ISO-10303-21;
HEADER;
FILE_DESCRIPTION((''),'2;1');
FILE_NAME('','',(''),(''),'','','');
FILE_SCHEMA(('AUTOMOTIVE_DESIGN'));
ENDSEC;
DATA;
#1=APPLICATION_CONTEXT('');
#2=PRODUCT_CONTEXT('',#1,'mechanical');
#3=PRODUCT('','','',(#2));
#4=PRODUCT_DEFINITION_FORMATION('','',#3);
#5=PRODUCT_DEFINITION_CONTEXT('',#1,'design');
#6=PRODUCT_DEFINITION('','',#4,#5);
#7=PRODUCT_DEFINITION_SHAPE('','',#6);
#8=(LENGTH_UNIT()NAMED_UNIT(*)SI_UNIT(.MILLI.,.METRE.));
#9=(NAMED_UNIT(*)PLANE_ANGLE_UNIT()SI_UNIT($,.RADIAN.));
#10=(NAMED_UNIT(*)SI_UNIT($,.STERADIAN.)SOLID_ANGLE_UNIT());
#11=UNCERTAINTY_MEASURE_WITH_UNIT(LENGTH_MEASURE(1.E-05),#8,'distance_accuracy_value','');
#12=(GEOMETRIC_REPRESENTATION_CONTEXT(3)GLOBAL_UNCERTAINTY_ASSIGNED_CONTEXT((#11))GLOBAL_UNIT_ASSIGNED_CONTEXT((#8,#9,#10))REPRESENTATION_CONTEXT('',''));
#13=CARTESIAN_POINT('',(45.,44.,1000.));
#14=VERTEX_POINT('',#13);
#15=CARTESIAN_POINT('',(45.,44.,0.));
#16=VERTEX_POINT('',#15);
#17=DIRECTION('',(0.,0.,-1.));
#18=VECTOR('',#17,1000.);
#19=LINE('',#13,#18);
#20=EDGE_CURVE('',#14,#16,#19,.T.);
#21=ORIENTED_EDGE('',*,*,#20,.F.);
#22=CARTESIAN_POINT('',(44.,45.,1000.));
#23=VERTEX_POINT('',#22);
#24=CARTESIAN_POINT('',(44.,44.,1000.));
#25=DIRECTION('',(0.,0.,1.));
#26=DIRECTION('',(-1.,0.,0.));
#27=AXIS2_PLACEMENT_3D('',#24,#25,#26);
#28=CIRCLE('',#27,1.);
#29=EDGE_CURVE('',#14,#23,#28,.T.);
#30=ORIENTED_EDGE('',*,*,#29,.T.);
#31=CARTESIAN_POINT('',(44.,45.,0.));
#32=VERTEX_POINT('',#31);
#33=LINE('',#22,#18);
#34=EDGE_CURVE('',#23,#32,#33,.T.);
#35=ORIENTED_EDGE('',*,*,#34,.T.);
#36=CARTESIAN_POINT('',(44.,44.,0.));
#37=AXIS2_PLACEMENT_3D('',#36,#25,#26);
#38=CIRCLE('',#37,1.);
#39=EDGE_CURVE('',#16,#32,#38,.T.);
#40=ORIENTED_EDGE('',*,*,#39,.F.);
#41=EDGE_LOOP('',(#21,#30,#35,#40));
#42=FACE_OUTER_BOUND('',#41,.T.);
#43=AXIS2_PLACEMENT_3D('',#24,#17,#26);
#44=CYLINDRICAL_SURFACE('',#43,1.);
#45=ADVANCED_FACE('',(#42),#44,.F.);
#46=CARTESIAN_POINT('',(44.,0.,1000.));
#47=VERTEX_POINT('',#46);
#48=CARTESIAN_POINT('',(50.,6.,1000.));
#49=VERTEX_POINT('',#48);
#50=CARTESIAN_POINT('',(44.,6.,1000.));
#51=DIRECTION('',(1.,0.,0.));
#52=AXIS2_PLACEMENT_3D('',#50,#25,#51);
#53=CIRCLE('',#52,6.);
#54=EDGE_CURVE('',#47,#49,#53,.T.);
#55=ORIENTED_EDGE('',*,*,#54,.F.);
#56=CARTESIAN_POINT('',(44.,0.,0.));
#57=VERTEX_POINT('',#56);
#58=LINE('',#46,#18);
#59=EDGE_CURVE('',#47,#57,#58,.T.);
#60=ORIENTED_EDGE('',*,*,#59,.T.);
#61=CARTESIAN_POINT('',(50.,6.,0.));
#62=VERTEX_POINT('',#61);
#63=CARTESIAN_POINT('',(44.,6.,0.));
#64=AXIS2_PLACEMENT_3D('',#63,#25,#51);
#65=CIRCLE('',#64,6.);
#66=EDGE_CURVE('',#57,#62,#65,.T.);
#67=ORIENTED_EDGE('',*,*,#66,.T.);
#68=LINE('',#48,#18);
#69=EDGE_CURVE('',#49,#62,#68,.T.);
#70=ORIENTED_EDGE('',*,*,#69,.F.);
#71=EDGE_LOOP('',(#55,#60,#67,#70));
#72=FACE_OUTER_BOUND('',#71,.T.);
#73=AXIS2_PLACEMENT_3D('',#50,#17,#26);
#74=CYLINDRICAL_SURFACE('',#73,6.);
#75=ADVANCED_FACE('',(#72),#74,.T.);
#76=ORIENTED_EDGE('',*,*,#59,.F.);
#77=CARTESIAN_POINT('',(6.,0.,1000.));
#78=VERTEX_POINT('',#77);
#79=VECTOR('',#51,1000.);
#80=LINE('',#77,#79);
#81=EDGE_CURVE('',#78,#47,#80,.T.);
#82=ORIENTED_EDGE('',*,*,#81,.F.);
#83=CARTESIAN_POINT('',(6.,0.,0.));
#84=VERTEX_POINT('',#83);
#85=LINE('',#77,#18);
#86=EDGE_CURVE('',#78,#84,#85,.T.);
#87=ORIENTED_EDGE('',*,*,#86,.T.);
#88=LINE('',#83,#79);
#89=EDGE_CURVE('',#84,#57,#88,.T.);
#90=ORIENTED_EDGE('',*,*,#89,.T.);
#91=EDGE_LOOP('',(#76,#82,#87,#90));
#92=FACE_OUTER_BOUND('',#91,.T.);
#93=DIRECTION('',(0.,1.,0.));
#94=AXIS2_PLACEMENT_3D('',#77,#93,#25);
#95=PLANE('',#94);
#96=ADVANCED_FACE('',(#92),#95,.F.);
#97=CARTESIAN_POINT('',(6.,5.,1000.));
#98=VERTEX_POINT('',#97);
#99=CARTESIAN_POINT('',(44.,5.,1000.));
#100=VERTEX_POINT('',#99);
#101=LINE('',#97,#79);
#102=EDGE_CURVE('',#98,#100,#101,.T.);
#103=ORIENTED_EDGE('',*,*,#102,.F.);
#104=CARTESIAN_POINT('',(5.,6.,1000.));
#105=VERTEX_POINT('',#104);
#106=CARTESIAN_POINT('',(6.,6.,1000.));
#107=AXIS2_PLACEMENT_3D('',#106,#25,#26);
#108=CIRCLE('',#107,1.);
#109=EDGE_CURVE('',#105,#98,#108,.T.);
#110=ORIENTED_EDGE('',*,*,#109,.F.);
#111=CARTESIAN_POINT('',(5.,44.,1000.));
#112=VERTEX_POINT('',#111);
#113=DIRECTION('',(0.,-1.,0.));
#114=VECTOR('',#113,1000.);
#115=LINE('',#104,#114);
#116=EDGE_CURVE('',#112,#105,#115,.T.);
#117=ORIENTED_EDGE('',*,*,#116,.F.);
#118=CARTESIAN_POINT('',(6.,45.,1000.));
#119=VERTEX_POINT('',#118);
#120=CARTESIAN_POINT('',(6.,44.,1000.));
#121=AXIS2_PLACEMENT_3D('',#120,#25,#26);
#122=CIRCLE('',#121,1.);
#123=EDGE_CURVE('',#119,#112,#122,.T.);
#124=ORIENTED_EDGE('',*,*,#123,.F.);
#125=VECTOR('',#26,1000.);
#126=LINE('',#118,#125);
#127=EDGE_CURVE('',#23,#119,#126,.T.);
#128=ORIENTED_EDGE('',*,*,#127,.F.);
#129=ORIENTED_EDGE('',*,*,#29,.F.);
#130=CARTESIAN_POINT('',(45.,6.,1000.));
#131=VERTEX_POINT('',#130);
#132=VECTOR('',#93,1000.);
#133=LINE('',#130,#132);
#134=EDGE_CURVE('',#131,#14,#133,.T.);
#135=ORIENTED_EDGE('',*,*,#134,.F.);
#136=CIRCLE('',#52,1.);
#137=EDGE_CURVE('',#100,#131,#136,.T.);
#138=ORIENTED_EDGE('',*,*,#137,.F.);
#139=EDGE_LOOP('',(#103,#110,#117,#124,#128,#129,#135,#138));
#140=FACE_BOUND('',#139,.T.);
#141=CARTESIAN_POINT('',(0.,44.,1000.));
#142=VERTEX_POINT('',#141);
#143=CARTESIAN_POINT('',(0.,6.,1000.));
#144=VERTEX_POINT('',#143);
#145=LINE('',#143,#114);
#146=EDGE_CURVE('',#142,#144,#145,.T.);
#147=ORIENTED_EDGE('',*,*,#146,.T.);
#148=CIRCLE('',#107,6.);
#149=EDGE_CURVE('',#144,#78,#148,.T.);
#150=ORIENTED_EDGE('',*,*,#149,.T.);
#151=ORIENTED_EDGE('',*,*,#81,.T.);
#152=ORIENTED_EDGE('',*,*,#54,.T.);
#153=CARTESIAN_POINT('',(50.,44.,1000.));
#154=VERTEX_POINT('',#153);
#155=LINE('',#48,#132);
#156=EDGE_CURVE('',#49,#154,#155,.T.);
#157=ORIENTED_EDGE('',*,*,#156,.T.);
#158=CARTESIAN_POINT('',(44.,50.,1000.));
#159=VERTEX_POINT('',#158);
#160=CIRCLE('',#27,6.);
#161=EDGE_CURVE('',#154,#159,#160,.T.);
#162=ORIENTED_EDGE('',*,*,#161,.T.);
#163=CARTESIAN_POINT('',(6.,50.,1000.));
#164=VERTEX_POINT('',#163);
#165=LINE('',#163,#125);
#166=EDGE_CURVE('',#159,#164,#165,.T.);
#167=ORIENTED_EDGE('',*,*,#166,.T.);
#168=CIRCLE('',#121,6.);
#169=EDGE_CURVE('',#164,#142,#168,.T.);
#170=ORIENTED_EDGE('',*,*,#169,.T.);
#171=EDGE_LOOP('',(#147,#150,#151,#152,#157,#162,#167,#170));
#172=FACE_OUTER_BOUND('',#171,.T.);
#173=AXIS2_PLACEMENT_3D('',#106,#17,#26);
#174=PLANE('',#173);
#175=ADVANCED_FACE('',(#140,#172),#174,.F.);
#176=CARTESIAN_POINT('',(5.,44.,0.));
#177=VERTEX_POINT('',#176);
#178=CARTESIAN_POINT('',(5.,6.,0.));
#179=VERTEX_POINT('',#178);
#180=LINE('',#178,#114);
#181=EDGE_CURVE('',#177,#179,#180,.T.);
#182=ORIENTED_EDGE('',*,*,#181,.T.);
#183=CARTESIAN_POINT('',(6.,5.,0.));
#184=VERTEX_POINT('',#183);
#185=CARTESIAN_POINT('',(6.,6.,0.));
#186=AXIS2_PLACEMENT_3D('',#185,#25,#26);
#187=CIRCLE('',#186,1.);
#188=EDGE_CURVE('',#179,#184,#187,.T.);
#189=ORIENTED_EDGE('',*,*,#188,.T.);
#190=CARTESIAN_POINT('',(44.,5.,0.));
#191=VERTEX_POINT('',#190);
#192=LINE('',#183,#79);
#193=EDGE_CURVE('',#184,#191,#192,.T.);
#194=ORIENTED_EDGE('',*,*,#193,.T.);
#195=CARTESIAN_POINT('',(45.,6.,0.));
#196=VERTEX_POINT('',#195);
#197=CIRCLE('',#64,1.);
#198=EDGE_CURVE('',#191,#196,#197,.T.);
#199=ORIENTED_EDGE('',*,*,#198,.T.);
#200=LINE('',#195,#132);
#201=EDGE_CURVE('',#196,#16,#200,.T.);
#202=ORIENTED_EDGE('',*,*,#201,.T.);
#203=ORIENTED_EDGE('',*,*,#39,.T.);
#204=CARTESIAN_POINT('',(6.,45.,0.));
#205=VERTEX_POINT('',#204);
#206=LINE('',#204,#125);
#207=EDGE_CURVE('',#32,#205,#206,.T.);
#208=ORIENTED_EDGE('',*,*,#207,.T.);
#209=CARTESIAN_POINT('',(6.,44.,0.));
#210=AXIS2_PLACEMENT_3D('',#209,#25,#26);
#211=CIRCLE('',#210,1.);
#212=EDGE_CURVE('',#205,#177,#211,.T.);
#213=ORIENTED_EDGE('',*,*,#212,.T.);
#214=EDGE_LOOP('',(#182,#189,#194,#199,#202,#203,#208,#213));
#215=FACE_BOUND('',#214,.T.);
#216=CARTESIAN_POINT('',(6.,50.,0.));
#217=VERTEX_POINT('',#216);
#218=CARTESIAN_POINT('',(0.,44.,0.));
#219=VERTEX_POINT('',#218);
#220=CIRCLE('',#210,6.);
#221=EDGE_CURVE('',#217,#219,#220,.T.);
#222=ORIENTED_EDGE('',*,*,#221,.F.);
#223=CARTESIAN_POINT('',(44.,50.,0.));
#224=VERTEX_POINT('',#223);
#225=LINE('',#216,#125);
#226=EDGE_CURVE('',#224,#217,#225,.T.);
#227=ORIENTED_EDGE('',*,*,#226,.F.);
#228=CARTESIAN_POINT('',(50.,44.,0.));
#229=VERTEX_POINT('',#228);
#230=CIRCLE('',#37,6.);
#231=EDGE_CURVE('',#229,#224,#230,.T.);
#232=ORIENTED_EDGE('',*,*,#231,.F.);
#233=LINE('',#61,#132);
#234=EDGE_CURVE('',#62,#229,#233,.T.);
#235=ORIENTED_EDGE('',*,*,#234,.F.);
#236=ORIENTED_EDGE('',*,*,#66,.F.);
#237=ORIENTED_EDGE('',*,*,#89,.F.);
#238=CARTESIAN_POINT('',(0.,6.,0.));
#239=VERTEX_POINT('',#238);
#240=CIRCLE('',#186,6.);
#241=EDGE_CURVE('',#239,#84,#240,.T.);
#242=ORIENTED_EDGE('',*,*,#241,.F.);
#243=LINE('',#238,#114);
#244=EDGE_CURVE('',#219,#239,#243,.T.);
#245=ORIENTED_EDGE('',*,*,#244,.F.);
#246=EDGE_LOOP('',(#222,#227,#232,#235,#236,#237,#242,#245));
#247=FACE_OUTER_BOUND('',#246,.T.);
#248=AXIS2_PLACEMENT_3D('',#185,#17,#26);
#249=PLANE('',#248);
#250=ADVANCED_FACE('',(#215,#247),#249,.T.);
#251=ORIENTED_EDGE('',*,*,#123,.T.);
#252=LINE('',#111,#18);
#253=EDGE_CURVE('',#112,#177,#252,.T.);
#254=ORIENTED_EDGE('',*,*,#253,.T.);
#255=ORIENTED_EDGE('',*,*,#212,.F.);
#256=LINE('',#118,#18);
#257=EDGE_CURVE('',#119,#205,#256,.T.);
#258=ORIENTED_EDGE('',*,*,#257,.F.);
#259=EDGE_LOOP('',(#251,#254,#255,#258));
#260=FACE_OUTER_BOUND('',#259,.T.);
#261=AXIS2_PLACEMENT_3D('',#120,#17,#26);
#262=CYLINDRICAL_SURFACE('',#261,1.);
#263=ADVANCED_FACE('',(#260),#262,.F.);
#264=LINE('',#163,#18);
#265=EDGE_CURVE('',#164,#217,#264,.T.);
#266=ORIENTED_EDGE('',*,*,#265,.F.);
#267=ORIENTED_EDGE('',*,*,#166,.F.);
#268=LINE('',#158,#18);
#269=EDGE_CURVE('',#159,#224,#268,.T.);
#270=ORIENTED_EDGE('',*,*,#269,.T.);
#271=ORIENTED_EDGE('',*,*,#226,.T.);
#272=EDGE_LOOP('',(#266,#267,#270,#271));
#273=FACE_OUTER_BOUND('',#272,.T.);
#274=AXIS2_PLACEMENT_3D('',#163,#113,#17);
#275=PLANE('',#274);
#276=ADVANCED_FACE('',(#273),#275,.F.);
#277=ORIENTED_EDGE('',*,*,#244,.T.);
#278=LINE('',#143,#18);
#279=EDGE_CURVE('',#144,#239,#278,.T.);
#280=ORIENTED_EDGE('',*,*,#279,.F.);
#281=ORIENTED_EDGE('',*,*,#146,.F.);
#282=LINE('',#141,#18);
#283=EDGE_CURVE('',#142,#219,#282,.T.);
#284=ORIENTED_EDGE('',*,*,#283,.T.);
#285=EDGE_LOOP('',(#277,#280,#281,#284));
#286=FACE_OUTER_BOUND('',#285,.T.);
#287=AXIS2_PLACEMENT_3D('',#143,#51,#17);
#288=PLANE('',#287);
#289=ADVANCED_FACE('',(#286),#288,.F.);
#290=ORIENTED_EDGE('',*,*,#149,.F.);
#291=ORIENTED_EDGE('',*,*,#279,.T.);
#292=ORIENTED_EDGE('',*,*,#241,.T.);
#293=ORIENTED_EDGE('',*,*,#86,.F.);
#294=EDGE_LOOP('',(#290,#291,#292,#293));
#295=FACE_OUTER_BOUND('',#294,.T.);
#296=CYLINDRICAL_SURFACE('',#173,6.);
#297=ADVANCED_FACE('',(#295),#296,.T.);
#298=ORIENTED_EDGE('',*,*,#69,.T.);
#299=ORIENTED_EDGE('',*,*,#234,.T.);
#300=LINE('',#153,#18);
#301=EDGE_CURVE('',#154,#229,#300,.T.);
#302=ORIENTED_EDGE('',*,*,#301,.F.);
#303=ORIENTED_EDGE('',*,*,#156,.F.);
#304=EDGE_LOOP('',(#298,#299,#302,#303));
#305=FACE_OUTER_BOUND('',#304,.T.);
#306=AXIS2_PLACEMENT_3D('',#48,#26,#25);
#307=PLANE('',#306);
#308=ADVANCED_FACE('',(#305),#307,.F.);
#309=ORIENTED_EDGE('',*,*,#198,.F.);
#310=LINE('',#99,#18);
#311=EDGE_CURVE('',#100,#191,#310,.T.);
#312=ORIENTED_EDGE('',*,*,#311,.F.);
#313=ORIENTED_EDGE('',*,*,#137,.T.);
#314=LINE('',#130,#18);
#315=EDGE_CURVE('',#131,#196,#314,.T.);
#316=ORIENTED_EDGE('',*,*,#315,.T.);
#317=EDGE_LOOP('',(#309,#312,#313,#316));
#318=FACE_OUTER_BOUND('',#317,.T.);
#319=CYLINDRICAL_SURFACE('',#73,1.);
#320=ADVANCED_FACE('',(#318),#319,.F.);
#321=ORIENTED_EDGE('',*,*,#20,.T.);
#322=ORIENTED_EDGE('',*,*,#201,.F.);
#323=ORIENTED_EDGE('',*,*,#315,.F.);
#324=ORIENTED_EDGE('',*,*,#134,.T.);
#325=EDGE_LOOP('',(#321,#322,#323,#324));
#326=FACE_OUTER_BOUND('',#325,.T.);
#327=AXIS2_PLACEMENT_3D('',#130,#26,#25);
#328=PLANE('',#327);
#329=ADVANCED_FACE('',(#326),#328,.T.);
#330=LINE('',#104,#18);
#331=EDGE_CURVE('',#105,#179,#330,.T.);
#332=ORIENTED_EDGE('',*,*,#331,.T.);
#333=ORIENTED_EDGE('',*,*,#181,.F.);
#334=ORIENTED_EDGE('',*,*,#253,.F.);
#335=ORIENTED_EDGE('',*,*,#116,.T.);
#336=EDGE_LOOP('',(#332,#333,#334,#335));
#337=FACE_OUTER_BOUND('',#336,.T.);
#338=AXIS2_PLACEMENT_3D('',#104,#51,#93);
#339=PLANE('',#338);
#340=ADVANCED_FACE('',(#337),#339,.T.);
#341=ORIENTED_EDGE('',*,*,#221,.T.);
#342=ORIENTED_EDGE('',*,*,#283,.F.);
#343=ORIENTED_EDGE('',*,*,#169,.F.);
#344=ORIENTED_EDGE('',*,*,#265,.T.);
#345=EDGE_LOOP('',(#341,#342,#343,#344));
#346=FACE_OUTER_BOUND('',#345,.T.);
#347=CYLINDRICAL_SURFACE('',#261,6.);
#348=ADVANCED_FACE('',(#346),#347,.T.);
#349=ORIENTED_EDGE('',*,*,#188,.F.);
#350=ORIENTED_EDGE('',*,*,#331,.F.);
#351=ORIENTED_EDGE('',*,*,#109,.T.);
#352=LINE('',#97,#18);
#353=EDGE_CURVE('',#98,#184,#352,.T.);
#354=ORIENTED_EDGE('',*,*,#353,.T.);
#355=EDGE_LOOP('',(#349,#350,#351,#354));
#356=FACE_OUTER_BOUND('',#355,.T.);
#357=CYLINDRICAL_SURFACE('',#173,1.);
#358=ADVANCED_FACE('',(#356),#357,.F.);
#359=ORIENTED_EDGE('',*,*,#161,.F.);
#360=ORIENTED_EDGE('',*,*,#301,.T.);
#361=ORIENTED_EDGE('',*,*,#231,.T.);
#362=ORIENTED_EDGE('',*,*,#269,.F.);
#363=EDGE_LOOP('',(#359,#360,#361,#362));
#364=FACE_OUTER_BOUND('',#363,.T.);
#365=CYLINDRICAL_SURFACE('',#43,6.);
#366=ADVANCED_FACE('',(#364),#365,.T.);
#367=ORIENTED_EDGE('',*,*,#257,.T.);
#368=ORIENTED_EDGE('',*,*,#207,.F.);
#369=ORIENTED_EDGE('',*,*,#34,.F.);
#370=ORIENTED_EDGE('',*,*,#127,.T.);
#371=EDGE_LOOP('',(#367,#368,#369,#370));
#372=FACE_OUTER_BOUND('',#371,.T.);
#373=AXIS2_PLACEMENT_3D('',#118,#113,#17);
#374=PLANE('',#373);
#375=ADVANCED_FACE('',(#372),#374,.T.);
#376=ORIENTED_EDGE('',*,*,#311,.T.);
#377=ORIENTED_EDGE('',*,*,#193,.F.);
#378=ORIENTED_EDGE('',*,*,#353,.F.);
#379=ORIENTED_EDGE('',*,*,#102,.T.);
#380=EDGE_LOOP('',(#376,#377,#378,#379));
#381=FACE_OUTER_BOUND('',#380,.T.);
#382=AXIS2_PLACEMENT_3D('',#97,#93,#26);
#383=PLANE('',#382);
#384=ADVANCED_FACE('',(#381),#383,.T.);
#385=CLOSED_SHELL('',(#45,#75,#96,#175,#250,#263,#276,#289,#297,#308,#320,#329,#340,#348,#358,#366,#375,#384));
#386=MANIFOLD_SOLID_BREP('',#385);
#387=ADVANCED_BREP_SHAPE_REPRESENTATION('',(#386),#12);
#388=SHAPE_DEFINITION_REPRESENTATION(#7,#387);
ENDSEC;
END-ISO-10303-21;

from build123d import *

# Parameters (mm, degrees)
BOSS_EXTRUDE1_DEPTH = 1000


with BuildPart() as part:
    # Sketch1 → Boss-Extrude1 (new body)
    with BuildSketch(Plane.XY):
        with BuildLine():
            Line((6, 0), (44, 0))
            ThreePointArc((44, 0), (48.242640687, 1.757359313), (50, 6))
            Line((50, 6), (50, 44))
            ThreePointArc((50, 44), (48.242640687, 48.242640687), (44, 50))
            Line((44, 50), (6, 50))
            ThreePointArc((6, 50), (1.757359313, 48.242640687), (0, 44))
            Line((0, 44), (0, 6))
            ThreePointArc((0, 6), (1.757359313, 1.757359313), (6, 0))
        make_face()
        with BuildLine():
            Line((6, 45), (44, 45))
            ThreePointArc((44, 45), (44.707106781, 44.707106781), (45, 44))
            Line((45, 44), (45, 6))
            ThreePointArc((45, 6), (44.707106781, 5.292893219), (44, 5))
            Line((44, 5), (6, 5))
            ThreePointArc((6, 5), (5.292893219, 5.292893219), (5, 6))
            Line((5, 6), (5, 44))
            ThreePointArc((5, 44), (5.292893219, 44.707106781), (6, 45))
        make_face(mode=Mode.SUBTRACT)
    extrude(amount=BOSS_EXTRUDE1_DEPTH)


solid = part.part
